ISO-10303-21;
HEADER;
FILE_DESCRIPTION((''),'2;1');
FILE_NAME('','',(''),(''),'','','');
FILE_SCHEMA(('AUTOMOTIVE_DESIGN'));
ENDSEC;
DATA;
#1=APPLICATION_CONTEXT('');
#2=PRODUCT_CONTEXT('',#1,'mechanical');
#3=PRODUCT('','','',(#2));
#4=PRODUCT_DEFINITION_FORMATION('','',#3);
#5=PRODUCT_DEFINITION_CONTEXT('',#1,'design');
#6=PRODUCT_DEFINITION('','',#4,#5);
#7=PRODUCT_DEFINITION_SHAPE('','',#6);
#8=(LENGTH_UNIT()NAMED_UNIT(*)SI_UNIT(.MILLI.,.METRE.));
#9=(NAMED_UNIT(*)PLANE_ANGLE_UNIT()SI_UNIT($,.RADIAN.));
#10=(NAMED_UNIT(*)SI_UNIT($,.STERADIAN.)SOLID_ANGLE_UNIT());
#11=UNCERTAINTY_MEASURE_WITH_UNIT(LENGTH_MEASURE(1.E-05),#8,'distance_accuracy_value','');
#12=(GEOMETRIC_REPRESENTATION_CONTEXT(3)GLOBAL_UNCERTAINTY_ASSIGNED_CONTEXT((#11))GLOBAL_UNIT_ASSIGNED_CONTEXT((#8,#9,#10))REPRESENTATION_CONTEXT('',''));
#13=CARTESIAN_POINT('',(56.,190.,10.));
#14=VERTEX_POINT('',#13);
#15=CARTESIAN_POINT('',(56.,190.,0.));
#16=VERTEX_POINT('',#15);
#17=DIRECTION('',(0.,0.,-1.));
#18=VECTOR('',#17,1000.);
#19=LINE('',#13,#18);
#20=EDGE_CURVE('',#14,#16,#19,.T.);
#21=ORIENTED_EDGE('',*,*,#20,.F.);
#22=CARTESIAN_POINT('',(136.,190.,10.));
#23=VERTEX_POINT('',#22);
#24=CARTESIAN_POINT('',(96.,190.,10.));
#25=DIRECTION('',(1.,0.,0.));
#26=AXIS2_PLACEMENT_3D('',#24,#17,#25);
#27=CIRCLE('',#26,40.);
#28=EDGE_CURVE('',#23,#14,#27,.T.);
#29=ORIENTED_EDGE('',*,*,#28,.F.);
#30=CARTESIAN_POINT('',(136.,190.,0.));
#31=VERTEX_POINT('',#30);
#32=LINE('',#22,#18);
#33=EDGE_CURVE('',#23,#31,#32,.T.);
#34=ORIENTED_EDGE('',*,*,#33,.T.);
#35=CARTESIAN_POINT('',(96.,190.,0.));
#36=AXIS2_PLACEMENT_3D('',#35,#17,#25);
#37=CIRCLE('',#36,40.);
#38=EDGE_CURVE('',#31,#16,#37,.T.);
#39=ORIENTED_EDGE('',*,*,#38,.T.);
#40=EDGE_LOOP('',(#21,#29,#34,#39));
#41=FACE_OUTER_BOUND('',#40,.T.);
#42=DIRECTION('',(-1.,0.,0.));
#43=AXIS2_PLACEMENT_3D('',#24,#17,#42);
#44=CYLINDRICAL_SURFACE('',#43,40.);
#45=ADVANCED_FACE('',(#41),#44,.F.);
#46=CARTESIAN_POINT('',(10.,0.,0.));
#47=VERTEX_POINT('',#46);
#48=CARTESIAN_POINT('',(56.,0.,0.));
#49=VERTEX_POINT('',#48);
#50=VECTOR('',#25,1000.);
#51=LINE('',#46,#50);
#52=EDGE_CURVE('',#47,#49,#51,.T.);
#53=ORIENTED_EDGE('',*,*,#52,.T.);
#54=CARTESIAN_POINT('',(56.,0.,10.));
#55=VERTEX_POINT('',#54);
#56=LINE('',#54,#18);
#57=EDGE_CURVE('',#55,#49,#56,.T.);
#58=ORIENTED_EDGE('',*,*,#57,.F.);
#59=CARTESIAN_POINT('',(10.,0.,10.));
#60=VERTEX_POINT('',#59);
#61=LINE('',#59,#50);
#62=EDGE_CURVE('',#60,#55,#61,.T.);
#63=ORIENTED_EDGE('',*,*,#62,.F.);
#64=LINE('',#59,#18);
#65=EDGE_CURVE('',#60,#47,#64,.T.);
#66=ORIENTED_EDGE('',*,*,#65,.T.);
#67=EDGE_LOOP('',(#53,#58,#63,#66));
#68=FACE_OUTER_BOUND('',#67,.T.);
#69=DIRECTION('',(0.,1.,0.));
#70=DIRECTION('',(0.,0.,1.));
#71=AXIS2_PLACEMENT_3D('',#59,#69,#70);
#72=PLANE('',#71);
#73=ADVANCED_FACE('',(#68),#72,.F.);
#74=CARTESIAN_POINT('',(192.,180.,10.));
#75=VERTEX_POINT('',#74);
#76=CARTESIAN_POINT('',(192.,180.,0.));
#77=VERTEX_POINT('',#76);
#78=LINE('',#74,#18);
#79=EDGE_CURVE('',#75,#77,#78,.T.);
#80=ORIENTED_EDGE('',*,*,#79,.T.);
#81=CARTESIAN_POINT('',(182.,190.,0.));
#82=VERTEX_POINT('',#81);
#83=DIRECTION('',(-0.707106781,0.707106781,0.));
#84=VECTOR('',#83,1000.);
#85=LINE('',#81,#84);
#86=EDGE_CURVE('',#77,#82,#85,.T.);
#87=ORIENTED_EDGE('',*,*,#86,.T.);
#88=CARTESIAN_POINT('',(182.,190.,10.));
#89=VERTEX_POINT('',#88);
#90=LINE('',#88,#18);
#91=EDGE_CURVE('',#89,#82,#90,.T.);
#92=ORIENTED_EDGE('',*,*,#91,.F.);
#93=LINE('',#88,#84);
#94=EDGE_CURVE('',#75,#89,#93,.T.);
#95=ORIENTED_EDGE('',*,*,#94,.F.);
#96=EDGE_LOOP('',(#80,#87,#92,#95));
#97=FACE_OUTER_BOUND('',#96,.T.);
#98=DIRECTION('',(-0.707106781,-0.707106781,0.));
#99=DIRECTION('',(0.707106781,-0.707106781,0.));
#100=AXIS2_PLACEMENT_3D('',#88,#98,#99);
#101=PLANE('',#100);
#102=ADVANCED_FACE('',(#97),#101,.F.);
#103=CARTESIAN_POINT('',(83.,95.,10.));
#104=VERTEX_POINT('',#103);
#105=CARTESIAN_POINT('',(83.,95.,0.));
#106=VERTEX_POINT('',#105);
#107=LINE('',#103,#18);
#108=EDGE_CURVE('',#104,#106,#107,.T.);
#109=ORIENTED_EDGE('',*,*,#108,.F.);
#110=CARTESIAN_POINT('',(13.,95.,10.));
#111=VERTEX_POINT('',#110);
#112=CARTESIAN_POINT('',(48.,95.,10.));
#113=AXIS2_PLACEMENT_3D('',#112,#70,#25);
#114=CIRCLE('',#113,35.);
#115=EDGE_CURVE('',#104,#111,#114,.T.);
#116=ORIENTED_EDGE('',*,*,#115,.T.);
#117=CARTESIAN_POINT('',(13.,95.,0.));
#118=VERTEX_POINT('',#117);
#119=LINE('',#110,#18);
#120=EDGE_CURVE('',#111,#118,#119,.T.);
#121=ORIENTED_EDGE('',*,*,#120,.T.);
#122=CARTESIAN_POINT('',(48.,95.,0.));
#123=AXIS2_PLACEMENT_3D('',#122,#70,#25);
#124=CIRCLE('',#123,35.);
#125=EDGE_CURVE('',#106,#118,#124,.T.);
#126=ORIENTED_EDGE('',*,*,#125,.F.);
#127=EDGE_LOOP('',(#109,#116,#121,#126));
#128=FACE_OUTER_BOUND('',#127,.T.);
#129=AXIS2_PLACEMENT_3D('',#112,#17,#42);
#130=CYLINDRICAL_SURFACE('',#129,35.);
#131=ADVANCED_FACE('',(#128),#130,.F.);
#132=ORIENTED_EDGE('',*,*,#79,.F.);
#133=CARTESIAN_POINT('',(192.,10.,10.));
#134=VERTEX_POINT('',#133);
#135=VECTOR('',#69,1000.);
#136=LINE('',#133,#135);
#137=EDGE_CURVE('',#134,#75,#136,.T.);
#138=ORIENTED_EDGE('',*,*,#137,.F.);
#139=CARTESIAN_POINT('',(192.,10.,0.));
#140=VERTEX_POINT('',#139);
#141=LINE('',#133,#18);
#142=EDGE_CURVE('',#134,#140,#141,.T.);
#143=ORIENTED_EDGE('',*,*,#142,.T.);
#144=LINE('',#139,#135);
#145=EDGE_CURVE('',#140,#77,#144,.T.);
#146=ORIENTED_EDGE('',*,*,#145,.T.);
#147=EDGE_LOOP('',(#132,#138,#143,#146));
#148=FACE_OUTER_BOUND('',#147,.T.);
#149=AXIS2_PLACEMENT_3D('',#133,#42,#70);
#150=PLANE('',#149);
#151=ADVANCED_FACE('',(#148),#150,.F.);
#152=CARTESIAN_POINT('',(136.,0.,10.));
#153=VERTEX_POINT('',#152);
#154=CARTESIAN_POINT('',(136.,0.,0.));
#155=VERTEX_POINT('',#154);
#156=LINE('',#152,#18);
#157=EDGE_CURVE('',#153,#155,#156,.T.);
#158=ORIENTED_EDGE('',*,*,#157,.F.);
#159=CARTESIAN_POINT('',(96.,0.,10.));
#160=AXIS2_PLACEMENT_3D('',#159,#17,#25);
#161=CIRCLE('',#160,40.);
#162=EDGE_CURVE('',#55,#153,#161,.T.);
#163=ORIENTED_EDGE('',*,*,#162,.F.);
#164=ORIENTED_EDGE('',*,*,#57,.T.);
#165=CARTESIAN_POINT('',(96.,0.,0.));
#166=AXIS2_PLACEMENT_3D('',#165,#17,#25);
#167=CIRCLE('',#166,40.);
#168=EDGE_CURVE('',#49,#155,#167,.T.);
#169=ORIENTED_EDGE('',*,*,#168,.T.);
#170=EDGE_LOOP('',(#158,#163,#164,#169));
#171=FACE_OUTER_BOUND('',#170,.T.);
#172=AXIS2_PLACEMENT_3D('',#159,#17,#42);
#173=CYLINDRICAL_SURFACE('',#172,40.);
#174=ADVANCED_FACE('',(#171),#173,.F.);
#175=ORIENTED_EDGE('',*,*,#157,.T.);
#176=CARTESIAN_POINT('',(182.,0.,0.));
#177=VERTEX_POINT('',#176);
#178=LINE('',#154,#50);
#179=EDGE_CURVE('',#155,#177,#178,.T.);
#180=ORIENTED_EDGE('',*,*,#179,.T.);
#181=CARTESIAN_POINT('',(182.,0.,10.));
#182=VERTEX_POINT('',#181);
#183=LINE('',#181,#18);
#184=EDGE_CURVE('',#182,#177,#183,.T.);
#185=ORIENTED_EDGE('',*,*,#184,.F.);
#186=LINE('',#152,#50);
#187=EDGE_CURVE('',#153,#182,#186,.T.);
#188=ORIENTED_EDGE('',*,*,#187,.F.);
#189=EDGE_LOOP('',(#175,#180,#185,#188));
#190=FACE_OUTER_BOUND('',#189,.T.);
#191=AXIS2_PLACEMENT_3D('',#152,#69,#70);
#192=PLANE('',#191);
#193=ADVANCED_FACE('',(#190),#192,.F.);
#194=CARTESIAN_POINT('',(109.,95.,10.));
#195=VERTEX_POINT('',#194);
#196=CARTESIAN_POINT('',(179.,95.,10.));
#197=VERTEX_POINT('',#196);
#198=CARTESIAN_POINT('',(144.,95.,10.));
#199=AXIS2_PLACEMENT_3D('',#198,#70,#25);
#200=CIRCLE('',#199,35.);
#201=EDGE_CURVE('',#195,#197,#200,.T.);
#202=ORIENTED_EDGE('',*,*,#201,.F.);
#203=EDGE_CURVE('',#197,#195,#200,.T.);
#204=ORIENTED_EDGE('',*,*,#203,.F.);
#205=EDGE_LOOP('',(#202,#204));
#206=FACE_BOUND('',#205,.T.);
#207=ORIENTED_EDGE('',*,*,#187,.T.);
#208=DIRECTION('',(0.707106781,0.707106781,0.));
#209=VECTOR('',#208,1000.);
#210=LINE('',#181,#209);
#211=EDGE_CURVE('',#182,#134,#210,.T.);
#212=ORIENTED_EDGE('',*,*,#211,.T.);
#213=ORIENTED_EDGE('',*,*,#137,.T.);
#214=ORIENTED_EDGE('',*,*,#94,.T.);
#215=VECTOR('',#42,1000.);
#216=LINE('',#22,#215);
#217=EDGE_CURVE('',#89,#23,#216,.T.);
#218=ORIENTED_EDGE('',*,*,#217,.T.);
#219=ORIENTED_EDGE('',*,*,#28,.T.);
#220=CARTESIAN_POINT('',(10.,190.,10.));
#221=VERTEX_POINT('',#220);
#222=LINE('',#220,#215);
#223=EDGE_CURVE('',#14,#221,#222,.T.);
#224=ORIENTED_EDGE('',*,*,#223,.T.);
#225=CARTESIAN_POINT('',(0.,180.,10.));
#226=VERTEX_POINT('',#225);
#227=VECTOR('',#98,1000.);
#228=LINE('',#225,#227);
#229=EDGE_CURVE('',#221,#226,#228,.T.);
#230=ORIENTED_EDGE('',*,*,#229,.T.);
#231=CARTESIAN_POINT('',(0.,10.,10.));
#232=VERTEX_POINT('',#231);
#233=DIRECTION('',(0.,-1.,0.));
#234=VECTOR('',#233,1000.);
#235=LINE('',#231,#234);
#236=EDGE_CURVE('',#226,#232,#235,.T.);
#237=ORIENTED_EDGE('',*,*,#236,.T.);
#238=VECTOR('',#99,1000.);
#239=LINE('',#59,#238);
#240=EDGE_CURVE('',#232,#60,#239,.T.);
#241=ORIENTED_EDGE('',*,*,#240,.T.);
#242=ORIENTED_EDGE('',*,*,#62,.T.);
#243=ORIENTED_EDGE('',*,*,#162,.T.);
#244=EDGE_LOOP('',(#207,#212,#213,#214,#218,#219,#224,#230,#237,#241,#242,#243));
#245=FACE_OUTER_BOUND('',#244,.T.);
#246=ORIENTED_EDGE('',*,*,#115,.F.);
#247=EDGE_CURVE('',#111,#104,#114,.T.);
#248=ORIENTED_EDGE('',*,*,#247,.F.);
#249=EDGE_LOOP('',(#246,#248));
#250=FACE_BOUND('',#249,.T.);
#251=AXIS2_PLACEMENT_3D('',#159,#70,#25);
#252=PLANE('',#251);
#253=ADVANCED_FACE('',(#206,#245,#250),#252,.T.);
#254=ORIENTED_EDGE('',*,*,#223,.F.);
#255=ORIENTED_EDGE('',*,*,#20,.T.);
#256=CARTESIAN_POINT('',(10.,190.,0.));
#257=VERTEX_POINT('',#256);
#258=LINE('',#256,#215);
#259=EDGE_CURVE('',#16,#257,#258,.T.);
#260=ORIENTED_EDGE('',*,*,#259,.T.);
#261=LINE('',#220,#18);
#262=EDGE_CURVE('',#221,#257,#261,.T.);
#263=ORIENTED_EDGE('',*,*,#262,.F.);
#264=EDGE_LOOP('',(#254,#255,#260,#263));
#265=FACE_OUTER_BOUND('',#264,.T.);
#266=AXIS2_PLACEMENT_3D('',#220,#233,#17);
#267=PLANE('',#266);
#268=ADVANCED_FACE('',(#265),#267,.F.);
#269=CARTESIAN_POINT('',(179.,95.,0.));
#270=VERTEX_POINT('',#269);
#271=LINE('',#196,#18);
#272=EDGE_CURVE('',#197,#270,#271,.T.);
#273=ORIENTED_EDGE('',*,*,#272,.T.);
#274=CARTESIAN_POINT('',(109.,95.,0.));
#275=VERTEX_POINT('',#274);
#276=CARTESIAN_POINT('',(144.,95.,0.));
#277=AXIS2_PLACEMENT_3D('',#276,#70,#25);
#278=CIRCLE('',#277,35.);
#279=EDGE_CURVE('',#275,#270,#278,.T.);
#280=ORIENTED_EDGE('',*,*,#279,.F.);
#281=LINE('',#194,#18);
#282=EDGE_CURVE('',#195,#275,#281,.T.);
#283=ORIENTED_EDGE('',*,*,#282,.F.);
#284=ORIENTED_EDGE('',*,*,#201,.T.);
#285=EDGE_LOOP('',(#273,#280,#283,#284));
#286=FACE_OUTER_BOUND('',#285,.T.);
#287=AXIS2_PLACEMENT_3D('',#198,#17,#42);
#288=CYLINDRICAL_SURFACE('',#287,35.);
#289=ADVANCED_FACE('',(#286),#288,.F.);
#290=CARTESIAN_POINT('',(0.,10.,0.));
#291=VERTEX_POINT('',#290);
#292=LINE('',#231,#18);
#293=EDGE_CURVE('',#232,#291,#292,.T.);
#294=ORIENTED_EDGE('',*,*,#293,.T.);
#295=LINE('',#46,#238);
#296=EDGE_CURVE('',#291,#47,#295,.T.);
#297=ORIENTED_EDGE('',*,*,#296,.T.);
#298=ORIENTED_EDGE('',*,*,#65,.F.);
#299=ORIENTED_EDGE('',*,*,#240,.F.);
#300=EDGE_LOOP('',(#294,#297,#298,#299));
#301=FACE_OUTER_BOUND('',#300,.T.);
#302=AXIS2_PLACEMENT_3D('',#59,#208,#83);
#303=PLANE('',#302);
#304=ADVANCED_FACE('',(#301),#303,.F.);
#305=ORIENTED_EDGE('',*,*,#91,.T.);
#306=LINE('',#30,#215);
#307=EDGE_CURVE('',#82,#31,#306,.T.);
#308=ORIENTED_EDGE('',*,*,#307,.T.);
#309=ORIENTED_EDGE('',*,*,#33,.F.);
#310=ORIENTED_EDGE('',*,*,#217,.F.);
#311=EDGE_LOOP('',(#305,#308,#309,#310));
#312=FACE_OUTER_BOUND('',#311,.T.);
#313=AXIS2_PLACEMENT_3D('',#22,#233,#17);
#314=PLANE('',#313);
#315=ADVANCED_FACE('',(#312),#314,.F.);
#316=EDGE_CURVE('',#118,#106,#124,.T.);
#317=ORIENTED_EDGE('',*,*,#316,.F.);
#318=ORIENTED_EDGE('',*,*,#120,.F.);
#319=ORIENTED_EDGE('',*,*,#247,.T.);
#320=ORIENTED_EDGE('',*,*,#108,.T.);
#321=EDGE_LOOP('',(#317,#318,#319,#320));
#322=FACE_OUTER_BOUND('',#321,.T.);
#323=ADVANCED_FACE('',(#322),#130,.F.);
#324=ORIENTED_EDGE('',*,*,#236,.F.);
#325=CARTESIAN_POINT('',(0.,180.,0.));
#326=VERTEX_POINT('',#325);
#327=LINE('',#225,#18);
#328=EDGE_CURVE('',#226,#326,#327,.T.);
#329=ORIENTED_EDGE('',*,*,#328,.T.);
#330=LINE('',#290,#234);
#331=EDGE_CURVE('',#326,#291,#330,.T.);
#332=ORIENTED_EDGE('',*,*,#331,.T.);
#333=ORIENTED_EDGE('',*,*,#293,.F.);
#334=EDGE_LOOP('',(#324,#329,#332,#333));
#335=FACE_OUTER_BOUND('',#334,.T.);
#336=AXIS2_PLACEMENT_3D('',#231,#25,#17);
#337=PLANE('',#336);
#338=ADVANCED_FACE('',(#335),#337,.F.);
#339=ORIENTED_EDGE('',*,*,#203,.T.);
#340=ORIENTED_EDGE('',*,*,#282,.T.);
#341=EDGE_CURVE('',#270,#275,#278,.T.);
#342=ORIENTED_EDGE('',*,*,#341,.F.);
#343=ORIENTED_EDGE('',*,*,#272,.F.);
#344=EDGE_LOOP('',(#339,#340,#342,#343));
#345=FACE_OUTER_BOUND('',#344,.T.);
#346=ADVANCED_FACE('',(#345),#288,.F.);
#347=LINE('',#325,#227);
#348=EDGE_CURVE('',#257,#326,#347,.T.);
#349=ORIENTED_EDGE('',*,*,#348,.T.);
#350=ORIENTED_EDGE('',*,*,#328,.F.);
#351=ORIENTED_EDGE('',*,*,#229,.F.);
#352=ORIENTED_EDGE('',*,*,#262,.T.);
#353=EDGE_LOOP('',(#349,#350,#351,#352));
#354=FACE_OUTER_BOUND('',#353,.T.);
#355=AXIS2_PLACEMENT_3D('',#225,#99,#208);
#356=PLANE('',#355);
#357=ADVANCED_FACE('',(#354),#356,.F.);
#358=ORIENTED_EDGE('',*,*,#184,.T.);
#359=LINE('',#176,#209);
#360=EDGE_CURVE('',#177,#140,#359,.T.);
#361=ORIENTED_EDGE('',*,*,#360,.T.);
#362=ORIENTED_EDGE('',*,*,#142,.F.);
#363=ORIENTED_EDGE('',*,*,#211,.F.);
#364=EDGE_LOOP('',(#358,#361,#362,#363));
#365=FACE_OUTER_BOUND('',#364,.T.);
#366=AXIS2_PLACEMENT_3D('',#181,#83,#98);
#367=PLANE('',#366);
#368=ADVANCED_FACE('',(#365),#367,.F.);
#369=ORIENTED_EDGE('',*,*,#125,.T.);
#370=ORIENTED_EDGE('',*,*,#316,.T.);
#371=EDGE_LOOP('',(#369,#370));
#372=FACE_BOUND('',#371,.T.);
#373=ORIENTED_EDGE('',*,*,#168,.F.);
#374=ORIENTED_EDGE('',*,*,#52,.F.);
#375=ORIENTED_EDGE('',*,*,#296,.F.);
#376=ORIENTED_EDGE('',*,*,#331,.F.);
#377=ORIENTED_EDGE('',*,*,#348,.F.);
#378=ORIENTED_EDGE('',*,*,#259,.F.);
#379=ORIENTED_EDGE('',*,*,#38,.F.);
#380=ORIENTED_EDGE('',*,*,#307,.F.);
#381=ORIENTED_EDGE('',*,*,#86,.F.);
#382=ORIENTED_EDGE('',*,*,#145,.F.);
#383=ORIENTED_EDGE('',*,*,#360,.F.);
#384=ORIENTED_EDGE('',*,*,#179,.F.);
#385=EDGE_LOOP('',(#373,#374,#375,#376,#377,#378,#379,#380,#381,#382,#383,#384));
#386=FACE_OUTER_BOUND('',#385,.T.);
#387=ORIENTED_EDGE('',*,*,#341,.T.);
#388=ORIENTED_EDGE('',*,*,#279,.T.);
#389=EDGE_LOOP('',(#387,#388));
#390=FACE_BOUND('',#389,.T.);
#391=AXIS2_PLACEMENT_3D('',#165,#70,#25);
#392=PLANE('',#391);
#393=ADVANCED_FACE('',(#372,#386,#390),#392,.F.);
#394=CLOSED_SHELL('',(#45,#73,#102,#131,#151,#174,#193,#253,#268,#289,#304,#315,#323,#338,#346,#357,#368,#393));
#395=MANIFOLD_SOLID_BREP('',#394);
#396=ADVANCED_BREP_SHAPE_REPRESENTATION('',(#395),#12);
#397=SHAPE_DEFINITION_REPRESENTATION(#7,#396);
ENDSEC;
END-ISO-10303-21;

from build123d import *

# Parameters (mm, degrees)
SKETCH1_R           = 35
BOSS_EXTRUDE1_DEPTH = 10


with BuildPart() as part:
    # Sketch1 → Boss-Extrude1 (new body)
    with BuildSketch(Plane.XY):
        with BuildLine():
            Line((10, 0), (56, 0))
            ThreePointArc((56, 0), (96, 40), (136, 0))
            Line((136, 0), (182, 0))
            Line((182, 0), (192, 10))
            Line((192, 10), (192, 180))
            Line((192, 180), (182, 190))
            Line((182, 190), (136, 190))
            ThreePointArc((136, 190), (96, 150), (56, 190))
            Line((56, 190), (10, 190))
            Line((10, 190), (0, 180))
            Line((0, 180), (0, 10))
            Line((0, 10), (10, 0))
        make_face()
        with Locations((48, 95)):
            Circle(SKETCH1_R, mode=Mode.SUBTRACT)
        with Locations((144, 95)):
            Circle(SKETCH1_R, mode=Mode.SUBTRACT)
    extrude(amount=BOSS_EXTRUDE1_DEPTH)


solid = part.part
